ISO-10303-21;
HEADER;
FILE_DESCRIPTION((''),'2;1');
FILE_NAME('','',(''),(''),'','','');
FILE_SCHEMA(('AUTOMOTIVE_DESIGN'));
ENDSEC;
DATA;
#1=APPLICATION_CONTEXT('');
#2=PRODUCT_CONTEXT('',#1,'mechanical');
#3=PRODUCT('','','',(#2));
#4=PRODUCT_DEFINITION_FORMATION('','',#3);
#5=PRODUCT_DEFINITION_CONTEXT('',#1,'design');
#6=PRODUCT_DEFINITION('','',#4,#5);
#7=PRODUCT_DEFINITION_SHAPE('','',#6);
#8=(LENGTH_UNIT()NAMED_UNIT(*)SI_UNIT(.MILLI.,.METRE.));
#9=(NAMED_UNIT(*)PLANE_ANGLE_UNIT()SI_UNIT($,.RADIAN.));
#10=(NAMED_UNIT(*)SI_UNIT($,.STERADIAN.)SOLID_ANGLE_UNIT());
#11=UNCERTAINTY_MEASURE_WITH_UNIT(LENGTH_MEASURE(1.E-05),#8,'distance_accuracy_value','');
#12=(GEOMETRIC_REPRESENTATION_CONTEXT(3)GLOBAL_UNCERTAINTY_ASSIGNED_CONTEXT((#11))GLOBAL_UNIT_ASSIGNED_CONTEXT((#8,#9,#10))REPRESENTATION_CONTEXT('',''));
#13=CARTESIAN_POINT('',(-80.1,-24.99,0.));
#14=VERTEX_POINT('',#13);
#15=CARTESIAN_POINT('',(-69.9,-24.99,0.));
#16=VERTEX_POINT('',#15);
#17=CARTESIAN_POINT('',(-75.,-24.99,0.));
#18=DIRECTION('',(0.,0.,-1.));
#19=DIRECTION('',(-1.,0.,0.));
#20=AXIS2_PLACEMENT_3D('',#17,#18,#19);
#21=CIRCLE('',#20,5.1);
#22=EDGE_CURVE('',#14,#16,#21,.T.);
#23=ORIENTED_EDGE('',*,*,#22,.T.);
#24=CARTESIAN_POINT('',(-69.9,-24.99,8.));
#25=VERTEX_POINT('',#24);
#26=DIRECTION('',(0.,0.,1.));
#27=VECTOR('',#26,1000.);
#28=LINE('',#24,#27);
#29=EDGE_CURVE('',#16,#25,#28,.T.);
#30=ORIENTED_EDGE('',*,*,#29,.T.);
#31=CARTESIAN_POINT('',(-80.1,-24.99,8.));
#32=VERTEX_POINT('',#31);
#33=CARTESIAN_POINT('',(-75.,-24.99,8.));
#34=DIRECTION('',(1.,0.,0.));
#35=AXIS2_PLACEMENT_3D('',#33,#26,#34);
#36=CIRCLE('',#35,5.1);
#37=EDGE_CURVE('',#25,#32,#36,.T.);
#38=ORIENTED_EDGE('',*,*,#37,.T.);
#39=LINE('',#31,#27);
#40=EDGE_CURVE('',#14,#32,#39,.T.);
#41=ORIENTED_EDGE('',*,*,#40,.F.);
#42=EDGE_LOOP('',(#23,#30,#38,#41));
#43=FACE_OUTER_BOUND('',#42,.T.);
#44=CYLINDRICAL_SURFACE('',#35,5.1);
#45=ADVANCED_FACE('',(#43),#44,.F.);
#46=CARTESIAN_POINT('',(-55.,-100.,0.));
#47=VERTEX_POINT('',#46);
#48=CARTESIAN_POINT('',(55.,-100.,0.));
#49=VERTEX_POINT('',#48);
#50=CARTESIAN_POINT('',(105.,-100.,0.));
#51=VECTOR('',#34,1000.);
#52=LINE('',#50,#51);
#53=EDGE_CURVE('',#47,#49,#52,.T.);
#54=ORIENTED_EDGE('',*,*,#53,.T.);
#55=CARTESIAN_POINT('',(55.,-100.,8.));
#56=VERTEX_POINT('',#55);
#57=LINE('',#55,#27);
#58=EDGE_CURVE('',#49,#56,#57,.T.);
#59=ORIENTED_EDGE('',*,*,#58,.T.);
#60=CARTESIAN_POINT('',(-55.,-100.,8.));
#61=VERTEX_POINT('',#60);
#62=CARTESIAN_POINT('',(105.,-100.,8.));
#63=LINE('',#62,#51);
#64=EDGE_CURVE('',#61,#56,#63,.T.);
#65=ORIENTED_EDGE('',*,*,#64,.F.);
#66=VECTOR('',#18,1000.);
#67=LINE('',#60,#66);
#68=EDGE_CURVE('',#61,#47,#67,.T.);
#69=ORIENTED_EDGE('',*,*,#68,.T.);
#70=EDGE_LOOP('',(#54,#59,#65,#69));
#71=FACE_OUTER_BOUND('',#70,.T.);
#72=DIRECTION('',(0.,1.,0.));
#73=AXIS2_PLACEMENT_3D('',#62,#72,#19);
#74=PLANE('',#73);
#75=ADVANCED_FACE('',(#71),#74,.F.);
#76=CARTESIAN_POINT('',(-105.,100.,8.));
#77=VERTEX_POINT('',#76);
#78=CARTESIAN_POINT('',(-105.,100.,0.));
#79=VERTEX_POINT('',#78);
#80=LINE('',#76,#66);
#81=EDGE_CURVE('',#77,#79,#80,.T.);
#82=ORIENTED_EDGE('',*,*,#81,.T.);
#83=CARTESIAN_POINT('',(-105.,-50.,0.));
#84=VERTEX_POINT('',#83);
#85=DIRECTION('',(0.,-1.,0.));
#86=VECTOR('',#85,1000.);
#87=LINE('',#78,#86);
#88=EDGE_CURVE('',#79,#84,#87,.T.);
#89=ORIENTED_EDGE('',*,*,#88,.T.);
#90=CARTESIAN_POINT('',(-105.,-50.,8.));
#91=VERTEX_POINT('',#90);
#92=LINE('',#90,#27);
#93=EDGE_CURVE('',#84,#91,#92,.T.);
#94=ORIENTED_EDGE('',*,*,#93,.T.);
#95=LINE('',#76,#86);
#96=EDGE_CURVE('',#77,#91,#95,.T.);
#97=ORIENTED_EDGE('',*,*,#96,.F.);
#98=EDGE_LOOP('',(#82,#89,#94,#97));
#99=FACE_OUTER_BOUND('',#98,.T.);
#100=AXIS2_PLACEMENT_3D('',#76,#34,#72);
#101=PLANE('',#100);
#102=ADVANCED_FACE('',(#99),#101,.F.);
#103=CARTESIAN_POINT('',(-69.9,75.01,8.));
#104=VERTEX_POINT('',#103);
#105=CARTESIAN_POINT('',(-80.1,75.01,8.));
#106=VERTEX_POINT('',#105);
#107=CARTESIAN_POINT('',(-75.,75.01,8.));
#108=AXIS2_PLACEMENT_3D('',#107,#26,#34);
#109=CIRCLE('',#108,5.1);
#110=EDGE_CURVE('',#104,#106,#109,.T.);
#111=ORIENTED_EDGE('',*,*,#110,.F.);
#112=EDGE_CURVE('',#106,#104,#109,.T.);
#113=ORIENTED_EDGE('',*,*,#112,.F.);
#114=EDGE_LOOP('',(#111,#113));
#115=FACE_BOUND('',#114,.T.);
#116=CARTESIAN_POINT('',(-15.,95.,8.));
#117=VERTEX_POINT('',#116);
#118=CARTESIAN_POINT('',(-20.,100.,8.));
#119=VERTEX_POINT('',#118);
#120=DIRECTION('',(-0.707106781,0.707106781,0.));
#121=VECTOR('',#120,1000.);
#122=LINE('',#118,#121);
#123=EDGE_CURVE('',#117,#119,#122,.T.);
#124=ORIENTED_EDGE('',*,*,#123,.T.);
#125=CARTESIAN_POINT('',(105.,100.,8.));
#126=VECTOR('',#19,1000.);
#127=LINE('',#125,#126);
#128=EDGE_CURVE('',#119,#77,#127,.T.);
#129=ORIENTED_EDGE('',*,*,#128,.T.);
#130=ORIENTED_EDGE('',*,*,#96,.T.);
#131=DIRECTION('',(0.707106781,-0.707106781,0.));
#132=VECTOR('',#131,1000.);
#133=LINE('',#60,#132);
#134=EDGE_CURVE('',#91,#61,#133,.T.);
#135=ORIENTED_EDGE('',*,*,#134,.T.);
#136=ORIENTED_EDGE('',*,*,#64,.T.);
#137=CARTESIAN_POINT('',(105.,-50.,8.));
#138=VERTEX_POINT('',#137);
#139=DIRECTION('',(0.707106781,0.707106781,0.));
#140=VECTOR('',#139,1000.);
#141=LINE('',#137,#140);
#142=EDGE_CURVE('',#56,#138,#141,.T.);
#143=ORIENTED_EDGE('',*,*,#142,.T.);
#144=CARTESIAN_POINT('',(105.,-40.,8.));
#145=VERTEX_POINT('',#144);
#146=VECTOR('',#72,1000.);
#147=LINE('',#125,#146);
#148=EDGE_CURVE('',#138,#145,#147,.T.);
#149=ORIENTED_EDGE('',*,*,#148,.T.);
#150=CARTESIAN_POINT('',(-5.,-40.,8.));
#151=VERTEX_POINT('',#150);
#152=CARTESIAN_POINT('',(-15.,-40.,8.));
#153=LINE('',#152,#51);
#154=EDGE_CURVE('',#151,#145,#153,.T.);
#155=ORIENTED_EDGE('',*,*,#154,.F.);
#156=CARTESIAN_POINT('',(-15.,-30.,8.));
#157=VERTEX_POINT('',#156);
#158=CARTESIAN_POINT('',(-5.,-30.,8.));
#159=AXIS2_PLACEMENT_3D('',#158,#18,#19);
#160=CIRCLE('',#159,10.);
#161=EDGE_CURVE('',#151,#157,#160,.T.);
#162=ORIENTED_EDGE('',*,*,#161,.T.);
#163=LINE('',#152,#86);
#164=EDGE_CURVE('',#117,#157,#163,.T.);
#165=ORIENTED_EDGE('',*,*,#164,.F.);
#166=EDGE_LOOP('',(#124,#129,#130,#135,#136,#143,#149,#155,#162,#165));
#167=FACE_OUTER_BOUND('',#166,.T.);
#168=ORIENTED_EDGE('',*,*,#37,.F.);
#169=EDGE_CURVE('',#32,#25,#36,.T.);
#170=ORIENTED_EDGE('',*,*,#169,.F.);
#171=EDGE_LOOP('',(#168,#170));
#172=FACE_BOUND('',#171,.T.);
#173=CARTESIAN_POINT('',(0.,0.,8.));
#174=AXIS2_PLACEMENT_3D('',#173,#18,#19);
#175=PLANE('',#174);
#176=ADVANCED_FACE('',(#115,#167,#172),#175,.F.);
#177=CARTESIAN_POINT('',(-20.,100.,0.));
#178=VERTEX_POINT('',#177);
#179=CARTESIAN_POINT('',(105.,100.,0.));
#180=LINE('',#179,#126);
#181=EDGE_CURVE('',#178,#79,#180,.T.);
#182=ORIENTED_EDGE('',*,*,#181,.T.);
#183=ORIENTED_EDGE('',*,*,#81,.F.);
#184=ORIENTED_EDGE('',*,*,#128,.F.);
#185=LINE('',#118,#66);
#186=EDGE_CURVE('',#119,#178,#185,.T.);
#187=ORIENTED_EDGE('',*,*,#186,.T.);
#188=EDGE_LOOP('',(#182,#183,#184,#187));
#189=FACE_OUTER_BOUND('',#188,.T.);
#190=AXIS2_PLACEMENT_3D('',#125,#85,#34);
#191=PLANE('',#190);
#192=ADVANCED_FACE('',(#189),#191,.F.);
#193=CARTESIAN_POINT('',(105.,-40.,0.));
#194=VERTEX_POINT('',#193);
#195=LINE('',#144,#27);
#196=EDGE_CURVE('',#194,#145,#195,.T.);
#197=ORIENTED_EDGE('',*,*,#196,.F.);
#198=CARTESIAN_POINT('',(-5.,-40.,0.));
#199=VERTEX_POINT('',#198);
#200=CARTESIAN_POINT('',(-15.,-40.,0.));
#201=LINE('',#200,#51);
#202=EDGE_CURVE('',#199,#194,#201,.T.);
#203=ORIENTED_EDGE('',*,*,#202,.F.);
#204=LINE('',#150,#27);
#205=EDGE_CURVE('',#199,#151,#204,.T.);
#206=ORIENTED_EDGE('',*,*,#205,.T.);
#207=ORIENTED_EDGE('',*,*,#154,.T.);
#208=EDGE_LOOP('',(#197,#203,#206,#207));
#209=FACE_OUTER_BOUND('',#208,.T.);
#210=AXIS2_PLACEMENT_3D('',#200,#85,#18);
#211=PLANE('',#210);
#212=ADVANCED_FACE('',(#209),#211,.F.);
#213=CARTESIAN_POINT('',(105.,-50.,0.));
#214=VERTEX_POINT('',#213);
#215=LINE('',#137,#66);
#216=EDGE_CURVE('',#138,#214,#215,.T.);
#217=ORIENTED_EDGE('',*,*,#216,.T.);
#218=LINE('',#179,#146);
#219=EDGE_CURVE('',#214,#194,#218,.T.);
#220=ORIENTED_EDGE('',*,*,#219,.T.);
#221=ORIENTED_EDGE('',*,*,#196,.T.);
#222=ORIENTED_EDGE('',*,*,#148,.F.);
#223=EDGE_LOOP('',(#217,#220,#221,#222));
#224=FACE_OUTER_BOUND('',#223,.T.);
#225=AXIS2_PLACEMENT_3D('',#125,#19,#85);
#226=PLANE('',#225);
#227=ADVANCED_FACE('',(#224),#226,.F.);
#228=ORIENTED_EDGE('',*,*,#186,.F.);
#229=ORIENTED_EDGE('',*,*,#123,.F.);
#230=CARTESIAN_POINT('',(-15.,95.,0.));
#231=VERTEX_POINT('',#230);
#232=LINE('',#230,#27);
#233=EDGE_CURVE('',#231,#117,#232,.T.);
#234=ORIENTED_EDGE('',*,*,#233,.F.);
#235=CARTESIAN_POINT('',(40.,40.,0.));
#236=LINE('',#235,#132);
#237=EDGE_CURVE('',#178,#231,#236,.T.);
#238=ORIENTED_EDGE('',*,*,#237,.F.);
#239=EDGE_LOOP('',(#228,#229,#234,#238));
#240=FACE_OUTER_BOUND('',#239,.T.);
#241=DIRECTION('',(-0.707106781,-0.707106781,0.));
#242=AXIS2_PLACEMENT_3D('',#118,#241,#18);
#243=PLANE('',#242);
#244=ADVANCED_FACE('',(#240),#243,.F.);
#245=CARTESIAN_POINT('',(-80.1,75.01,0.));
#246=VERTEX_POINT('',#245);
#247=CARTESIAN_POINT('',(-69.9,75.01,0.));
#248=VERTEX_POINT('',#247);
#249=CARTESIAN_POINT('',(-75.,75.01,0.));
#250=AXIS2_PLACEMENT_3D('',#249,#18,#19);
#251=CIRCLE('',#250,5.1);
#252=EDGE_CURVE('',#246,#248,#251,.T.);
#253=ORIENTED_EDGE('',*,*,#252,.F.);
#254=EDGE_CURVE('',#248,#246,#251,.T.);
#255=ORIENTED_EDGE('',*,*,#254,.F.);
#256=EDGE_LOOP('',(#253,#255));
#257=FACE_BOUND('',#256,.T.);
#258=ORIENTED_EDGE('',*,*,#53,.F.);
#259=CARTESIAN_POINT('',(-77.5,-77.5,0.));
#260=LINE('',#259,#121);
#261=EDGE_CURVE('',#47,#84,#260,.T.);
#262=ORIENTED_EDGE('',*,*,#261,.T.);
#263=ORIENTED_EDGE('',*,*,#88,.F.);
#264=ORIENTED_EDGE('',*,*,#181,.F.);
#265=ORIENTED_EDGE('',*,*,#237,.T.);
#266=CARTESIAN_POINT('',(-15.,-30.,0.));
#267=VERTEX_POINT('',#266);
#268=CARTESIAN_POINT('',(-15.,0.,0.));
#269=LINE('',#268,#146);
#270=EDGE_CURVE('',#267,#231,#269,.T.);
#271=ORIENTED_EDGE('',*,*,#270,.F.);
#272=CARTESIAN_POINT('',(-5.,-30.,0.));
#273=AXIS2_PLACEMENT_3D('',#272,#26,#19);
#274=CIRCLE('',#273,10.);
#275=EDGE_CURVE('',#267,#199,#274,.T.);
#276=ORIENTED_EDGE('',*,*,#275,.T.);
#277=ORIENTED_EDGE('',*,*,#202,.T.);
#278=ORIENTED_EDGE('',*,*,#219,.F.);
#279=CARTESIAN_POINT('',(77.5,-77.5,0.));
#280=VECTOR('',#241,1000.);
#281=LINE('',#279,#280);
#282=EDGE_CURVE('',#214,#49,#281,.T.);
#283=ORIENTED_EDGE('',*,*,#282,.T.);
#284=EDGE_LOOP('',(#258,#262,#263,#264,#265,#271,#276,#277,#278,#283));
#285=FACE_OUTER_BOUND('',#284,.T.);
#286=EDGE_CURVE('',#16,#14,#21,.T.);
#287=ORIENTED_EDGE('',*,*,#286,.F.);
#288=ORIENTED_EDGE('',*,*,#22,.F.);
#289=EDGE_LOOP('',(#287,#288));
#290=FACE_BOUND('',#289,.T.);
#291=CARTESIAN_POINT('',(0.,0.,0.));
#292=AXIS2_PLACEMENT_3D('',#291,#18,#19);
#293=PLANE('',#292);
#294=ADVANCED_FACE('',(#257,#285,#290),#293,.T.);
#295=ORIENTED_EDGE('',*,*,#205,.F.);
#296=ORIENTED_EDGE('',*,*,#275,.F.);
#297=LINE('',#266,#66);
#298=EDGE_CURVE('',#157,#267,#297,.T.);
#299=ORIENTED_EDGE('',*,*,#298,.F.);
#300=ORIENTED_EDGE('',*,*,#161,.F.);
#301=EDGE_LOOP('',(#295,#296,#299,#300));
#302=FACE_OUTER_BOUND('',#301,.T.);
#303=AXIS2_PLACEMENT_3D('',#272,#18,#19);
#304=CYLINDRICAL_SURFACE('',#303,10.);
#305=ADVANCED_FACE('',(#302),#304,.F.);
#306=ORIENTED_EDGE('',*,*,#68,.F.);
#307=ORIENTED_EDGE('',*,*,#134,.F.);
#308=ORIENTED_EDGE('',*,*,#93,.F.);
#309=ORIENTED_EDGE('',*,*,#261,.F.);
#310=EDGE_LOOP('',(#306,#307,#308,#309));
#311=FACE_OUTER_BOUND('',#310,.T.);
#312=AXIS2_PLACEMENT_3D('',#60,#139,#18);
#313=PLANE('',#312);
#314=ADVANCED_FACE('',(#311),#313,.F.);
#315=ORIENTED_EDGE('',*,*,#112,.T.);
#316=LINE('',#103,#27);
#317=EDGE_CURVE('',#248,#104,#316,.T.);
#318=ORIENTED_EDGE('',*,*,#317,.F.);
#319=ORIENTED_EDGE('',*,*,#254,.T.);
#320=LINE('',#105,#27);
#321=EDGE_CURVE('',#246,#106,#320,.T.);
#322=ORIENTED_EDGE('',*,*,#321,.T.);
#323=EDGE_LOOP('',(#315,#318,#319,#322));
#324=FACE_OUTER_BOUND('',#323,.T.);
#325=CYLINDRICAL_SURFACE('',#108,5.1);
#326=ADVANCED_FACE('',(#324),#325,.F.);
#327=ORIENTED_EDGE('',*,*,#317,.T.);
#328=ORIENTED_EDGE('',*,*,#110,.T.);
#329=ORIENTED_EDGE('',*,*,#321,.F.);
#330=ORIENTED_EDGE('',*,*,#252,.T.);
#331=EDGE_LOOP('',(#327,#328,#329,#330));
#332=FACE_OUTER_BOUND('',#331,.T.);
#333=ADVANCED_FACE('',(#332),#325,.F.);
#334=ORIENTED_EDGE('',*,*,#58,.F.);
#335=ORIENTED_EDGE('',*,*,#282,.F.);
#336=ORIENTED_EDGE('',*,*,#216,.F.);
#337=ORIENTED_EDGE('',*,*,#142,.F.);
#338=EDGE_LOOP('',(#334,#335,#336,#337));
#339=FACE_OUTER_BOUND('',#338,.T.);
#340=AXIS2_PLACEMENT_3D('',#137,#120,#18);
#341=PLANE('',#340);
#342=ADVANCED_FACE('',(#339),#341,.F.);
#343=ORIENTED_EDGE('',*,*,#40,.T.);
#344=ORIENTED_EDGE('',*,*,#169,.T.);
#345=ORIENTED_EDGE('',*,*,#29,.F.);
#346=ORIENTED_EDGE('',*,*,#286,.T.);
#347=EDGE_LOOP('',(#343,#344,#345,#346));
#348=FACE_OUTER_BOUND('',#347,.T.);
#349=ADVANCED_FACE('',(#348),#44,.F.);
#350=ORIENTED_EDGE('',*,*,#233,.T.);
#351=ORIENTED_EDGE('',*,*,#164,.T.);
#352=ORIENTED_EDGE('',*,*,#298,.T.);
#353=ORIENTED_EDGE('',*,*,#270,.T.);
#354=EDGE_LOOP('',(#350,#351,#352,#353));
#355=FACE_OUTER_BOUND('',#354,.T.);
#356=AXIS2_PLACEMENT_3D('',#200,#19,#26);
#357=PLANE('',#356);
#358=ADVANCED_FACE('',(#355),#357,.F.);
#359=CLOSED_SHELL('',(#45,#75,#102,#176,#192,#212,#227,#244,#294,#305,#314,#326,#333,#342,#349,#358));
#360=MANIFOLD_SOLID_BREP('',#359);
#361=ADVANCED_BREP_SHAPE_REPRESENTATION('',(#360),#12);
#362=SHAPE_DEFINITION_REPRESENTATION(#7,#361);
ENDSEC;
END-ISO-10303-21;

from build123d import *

# Parameters (mm, degrees)
SKETCH1_W              = 210
SKETCH1_H              = 200
BOSS_EXTRUDE1_DEPTH    = 8
CHAMFER1_SIZE          = 50
M12_TAPPED_HOLE1_D     = 10.2
M12_TAPPED_HOLE1_DEPTH = 29.25
M12_TAPPED_HOLE1_TIP   = 3.064389157
SKETCH5_W              = 180.548294757
SKETCH5_H              = 165.829683772
CUT_EXTRUDE1_DEPTH     = 8
CHAMFER2_SIZE          = 5
FILLET1_R              = 10


with BuildPart() as part:
    # Sketch1 → Boss-Extrude1 (new body)
    with BuildSketch(Plane.XY):
        Rectangle(SKETCH1_W, SKETCH1_H)
    extrude(amount=BOSS_EXTRUDE1_DEPTH)

    # Chamfer1
    chamfer1_edges = [part.edges().sort_by_distance(p)[0] for p in [
        (105, -100, 4),
        (-105, -100, 4),
    ]]
    chamfer(chamfer1_edges, length=CHAMFER1_SIZE)

    # M12 Tapped Hole1
    with Locations(Plane.XY.offset(8)):
        with Locations((-75, 75.01), (-75, -24.99)):
            Hole(M12_TAPPED_HOLE1_D / 2, depth=M12_TAPPED_HOLE1_DEPTH)
            with Locations((0, 0, -(M12_TAPPED_HOLE1_DEPTH + M12_TAPPED_HOLE1_TIP / 2))):  # 118° drill point
                Cone(0, M12_TAPPED_HOLE1_D / 2, M12_TAPPED_HOLE1_TIP, mode=Mode.SUBTRACT)

    # Sketch5 → Cut-Extrude1 (cut)
    with BuildSketch(Plane.XY.offset(8)):
        with Locations((75.274147379, 42.914841886)):
            Rectangle(SKETCH5_W, SKETCH5_H)
    extrude(amount=-CUT_EXTRUDE1_DEPTH, mode=Mode.SUBTRACT)

    # Chamfer2
    chamfer2_edges = [part.edges().sort_by_distance(p)[0] for p in [
        (-15, 100, 4),
    ]]
    chamfer(chamfer2_edges, length=CHAMFER2_SIZE)

    # Fillet1
    fillet1_edges = [part.edges().sort_by_distance(p)[0] for p in [
        (-15, -40, 4),
    ]]
    fillet(fillet1_edges, radius=FILLET1_R)


solid = part.part
